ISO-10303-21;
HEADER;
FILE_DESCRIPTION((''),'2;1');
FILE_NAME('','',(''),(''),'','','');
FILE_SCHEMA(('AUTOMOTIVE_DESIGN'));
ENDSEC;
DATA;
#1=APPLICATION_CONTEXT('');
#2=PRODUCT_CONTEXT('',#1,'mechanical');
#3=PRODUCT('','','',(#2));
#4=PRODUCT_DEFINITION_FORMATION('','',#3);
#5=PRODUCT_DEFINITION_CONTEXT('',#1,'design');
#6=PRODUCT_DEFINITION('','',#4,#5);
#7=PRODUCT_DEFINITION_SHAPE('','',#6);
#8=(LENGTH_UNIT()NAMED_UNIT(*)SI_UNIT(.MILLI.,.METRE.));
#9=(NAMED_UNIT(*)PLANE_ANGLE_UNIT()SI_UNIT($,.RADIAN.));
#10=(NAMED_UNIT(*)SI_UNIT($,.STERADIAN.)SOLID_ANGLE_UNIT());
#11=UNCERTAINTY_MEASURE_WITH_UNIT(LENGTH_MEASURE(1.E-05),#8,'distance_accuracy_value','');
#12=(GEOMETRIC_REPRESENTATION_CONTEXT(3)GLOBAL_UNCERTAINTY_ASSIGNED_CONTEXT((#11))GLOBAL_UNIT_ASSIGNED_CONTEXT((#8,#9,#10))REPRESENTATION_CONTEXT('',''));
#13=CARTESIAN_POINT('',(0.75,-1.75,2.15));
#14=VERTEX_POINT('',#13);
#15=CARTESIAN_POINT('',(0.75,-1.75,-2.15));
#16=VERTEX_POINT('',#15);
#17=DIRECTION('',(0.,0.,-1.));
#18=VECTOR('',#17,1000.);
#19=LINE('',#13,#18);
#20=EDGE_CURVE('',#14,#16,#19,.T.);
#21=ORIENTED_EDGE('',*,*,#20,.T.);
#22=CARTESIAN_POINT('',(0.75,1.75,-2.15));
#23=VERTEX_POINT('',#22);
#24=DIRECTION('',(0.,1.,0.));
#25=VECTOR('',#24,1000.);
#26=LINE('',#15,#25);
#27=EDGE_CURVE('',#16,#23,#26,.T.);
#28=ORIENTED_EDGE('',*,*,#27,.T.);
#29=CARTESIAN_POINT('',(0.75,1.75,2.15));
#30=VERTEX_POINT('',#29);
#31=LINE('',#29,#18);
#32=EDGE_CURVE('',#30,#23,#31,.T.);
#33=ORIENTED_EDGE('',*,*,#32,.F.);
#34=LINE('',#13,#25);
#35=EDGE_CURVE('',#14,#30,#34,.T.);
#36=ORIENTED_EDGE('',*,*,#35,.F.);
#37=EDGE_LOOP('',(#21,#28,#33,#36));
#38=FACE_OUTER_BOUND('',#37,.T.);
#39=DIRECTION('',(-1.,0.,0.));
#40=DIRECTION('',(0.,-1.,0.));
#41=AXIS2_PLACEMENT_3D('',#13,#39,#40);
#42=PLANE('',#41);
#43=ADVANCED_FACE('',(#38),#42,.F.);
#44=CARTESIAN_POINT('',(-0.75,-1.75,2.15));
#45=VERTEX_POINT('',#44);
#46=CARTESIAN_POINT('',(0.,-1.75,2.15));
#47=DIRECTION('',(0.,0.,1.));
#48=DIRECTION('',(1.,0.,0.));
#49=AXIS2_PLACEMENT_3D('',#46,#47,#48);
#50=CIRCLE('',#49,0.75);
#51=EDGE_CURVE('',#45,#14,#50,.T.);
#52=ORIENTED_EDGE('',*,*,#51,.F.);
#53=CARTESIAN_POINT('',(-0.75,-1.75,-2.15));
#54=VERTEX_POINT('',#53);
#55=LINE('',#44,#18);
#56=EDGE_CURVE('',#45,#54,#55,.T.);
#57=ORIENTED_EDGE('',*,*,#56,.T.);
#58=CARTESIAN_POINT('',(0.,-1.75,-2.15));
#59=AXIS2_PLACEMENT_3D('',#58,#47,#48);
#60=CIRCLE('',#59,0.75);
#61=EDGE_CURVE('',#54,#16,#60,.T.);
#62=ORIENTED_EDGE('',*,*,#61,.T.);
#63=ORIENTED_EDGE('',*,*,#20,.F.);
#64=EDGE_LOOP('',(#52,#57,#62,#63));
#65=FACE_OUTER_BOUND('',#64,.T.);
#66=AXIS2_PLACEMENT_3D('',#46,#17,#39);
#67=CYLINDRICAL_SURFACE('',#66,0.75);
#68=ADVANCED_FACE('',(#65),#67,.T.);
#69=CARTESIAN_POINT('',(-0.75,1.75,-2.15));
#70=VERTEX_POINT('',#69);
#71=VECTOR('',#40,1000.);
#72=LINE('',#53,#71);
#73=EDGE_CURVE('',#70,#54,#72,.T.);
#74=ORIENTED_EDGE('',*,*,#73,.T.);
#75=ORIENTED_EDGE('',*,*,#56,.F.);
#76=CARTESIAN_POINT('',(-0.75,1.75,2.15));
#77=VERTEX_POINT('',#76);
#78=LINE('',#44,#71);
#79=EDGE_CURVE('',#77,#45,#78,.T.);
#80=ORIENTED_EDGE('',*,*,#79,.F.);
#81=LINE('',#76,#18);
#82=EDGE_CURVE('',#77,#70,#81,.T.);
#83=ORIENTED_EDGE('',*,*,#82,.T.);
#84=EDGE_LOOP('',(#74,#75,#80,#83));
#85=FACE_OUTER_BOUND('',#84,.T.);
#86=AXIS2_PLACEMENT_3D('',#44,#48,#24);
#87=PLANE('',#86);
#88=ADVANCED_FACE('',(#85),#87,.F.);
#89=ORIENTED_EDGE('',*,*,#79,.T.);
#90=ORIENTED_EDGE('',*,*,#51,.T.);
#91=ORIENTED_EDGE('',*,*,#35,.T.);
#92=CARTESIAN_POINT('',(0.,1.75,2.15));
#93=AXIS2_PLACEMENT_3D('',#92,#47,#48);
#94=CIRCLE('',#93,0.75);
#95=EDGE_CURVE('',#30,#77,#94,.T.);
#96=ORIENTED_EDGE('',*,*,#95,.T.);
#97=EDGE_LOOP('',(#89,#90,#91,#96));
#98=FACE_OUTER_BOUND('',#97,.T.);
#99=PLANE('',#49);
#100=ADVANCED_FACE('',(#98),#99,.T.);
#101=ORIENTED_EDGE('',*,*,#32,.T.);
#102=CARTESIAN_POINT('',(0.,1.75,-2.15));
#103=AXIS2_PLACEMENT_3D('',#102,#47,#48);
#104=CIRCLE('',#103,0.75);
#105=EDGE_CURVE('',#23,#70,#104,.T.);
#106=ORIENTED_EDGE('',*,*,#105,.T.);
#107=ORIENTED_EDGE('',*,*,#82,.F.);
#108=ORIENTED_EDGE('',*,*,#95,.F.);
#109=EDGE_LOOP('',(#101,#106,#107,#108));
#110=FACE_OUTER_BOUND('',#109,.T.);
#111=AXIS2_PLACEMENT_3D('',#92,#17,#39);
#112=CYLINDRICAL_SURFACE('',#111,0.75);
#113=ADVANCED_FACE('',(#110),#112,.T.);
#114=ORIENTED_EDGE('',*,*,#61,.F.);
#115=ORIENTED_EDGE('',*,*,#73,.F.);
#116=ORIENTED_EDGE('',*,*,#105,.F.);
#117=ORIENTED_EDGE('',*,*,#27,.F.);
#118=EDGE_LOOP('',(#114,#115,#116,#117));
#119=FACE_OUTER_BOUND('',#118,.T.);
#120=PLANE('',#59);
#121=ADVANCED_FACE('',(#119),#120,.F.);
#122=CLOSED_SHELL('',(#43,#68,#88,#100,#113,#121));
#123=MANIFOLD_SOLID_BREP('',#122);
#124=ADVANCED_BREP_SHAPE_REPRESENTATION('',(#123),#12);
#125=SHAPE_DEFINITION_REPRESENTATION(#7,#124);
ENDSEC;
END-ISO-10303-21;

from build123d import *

# Parameters (mm, degrees)
EXTRUDE_1_DEPTH = 2.15


with BuildPart() as part:
    # 草图1 → 凸台-拉伸1 (new, symmetric)
    with BuildSketch(Plane.XY):
        with BuildLine():
            Line((-0.75, -1.75), (-0.75, 1.75))
            ThreePointArc((-0.75, 1.75), (0, 2.5), (0.75, 1.75))
            Line((0.75, 1.75), (0.75, -1.75))
            ThreePointArc((0.75, -1.75), (0, -2.5), (-0.75, -1.75))
        make_face()
    extrude(amount=EXTRUDE_1_DEPTH, both=True)


solid = part.part
